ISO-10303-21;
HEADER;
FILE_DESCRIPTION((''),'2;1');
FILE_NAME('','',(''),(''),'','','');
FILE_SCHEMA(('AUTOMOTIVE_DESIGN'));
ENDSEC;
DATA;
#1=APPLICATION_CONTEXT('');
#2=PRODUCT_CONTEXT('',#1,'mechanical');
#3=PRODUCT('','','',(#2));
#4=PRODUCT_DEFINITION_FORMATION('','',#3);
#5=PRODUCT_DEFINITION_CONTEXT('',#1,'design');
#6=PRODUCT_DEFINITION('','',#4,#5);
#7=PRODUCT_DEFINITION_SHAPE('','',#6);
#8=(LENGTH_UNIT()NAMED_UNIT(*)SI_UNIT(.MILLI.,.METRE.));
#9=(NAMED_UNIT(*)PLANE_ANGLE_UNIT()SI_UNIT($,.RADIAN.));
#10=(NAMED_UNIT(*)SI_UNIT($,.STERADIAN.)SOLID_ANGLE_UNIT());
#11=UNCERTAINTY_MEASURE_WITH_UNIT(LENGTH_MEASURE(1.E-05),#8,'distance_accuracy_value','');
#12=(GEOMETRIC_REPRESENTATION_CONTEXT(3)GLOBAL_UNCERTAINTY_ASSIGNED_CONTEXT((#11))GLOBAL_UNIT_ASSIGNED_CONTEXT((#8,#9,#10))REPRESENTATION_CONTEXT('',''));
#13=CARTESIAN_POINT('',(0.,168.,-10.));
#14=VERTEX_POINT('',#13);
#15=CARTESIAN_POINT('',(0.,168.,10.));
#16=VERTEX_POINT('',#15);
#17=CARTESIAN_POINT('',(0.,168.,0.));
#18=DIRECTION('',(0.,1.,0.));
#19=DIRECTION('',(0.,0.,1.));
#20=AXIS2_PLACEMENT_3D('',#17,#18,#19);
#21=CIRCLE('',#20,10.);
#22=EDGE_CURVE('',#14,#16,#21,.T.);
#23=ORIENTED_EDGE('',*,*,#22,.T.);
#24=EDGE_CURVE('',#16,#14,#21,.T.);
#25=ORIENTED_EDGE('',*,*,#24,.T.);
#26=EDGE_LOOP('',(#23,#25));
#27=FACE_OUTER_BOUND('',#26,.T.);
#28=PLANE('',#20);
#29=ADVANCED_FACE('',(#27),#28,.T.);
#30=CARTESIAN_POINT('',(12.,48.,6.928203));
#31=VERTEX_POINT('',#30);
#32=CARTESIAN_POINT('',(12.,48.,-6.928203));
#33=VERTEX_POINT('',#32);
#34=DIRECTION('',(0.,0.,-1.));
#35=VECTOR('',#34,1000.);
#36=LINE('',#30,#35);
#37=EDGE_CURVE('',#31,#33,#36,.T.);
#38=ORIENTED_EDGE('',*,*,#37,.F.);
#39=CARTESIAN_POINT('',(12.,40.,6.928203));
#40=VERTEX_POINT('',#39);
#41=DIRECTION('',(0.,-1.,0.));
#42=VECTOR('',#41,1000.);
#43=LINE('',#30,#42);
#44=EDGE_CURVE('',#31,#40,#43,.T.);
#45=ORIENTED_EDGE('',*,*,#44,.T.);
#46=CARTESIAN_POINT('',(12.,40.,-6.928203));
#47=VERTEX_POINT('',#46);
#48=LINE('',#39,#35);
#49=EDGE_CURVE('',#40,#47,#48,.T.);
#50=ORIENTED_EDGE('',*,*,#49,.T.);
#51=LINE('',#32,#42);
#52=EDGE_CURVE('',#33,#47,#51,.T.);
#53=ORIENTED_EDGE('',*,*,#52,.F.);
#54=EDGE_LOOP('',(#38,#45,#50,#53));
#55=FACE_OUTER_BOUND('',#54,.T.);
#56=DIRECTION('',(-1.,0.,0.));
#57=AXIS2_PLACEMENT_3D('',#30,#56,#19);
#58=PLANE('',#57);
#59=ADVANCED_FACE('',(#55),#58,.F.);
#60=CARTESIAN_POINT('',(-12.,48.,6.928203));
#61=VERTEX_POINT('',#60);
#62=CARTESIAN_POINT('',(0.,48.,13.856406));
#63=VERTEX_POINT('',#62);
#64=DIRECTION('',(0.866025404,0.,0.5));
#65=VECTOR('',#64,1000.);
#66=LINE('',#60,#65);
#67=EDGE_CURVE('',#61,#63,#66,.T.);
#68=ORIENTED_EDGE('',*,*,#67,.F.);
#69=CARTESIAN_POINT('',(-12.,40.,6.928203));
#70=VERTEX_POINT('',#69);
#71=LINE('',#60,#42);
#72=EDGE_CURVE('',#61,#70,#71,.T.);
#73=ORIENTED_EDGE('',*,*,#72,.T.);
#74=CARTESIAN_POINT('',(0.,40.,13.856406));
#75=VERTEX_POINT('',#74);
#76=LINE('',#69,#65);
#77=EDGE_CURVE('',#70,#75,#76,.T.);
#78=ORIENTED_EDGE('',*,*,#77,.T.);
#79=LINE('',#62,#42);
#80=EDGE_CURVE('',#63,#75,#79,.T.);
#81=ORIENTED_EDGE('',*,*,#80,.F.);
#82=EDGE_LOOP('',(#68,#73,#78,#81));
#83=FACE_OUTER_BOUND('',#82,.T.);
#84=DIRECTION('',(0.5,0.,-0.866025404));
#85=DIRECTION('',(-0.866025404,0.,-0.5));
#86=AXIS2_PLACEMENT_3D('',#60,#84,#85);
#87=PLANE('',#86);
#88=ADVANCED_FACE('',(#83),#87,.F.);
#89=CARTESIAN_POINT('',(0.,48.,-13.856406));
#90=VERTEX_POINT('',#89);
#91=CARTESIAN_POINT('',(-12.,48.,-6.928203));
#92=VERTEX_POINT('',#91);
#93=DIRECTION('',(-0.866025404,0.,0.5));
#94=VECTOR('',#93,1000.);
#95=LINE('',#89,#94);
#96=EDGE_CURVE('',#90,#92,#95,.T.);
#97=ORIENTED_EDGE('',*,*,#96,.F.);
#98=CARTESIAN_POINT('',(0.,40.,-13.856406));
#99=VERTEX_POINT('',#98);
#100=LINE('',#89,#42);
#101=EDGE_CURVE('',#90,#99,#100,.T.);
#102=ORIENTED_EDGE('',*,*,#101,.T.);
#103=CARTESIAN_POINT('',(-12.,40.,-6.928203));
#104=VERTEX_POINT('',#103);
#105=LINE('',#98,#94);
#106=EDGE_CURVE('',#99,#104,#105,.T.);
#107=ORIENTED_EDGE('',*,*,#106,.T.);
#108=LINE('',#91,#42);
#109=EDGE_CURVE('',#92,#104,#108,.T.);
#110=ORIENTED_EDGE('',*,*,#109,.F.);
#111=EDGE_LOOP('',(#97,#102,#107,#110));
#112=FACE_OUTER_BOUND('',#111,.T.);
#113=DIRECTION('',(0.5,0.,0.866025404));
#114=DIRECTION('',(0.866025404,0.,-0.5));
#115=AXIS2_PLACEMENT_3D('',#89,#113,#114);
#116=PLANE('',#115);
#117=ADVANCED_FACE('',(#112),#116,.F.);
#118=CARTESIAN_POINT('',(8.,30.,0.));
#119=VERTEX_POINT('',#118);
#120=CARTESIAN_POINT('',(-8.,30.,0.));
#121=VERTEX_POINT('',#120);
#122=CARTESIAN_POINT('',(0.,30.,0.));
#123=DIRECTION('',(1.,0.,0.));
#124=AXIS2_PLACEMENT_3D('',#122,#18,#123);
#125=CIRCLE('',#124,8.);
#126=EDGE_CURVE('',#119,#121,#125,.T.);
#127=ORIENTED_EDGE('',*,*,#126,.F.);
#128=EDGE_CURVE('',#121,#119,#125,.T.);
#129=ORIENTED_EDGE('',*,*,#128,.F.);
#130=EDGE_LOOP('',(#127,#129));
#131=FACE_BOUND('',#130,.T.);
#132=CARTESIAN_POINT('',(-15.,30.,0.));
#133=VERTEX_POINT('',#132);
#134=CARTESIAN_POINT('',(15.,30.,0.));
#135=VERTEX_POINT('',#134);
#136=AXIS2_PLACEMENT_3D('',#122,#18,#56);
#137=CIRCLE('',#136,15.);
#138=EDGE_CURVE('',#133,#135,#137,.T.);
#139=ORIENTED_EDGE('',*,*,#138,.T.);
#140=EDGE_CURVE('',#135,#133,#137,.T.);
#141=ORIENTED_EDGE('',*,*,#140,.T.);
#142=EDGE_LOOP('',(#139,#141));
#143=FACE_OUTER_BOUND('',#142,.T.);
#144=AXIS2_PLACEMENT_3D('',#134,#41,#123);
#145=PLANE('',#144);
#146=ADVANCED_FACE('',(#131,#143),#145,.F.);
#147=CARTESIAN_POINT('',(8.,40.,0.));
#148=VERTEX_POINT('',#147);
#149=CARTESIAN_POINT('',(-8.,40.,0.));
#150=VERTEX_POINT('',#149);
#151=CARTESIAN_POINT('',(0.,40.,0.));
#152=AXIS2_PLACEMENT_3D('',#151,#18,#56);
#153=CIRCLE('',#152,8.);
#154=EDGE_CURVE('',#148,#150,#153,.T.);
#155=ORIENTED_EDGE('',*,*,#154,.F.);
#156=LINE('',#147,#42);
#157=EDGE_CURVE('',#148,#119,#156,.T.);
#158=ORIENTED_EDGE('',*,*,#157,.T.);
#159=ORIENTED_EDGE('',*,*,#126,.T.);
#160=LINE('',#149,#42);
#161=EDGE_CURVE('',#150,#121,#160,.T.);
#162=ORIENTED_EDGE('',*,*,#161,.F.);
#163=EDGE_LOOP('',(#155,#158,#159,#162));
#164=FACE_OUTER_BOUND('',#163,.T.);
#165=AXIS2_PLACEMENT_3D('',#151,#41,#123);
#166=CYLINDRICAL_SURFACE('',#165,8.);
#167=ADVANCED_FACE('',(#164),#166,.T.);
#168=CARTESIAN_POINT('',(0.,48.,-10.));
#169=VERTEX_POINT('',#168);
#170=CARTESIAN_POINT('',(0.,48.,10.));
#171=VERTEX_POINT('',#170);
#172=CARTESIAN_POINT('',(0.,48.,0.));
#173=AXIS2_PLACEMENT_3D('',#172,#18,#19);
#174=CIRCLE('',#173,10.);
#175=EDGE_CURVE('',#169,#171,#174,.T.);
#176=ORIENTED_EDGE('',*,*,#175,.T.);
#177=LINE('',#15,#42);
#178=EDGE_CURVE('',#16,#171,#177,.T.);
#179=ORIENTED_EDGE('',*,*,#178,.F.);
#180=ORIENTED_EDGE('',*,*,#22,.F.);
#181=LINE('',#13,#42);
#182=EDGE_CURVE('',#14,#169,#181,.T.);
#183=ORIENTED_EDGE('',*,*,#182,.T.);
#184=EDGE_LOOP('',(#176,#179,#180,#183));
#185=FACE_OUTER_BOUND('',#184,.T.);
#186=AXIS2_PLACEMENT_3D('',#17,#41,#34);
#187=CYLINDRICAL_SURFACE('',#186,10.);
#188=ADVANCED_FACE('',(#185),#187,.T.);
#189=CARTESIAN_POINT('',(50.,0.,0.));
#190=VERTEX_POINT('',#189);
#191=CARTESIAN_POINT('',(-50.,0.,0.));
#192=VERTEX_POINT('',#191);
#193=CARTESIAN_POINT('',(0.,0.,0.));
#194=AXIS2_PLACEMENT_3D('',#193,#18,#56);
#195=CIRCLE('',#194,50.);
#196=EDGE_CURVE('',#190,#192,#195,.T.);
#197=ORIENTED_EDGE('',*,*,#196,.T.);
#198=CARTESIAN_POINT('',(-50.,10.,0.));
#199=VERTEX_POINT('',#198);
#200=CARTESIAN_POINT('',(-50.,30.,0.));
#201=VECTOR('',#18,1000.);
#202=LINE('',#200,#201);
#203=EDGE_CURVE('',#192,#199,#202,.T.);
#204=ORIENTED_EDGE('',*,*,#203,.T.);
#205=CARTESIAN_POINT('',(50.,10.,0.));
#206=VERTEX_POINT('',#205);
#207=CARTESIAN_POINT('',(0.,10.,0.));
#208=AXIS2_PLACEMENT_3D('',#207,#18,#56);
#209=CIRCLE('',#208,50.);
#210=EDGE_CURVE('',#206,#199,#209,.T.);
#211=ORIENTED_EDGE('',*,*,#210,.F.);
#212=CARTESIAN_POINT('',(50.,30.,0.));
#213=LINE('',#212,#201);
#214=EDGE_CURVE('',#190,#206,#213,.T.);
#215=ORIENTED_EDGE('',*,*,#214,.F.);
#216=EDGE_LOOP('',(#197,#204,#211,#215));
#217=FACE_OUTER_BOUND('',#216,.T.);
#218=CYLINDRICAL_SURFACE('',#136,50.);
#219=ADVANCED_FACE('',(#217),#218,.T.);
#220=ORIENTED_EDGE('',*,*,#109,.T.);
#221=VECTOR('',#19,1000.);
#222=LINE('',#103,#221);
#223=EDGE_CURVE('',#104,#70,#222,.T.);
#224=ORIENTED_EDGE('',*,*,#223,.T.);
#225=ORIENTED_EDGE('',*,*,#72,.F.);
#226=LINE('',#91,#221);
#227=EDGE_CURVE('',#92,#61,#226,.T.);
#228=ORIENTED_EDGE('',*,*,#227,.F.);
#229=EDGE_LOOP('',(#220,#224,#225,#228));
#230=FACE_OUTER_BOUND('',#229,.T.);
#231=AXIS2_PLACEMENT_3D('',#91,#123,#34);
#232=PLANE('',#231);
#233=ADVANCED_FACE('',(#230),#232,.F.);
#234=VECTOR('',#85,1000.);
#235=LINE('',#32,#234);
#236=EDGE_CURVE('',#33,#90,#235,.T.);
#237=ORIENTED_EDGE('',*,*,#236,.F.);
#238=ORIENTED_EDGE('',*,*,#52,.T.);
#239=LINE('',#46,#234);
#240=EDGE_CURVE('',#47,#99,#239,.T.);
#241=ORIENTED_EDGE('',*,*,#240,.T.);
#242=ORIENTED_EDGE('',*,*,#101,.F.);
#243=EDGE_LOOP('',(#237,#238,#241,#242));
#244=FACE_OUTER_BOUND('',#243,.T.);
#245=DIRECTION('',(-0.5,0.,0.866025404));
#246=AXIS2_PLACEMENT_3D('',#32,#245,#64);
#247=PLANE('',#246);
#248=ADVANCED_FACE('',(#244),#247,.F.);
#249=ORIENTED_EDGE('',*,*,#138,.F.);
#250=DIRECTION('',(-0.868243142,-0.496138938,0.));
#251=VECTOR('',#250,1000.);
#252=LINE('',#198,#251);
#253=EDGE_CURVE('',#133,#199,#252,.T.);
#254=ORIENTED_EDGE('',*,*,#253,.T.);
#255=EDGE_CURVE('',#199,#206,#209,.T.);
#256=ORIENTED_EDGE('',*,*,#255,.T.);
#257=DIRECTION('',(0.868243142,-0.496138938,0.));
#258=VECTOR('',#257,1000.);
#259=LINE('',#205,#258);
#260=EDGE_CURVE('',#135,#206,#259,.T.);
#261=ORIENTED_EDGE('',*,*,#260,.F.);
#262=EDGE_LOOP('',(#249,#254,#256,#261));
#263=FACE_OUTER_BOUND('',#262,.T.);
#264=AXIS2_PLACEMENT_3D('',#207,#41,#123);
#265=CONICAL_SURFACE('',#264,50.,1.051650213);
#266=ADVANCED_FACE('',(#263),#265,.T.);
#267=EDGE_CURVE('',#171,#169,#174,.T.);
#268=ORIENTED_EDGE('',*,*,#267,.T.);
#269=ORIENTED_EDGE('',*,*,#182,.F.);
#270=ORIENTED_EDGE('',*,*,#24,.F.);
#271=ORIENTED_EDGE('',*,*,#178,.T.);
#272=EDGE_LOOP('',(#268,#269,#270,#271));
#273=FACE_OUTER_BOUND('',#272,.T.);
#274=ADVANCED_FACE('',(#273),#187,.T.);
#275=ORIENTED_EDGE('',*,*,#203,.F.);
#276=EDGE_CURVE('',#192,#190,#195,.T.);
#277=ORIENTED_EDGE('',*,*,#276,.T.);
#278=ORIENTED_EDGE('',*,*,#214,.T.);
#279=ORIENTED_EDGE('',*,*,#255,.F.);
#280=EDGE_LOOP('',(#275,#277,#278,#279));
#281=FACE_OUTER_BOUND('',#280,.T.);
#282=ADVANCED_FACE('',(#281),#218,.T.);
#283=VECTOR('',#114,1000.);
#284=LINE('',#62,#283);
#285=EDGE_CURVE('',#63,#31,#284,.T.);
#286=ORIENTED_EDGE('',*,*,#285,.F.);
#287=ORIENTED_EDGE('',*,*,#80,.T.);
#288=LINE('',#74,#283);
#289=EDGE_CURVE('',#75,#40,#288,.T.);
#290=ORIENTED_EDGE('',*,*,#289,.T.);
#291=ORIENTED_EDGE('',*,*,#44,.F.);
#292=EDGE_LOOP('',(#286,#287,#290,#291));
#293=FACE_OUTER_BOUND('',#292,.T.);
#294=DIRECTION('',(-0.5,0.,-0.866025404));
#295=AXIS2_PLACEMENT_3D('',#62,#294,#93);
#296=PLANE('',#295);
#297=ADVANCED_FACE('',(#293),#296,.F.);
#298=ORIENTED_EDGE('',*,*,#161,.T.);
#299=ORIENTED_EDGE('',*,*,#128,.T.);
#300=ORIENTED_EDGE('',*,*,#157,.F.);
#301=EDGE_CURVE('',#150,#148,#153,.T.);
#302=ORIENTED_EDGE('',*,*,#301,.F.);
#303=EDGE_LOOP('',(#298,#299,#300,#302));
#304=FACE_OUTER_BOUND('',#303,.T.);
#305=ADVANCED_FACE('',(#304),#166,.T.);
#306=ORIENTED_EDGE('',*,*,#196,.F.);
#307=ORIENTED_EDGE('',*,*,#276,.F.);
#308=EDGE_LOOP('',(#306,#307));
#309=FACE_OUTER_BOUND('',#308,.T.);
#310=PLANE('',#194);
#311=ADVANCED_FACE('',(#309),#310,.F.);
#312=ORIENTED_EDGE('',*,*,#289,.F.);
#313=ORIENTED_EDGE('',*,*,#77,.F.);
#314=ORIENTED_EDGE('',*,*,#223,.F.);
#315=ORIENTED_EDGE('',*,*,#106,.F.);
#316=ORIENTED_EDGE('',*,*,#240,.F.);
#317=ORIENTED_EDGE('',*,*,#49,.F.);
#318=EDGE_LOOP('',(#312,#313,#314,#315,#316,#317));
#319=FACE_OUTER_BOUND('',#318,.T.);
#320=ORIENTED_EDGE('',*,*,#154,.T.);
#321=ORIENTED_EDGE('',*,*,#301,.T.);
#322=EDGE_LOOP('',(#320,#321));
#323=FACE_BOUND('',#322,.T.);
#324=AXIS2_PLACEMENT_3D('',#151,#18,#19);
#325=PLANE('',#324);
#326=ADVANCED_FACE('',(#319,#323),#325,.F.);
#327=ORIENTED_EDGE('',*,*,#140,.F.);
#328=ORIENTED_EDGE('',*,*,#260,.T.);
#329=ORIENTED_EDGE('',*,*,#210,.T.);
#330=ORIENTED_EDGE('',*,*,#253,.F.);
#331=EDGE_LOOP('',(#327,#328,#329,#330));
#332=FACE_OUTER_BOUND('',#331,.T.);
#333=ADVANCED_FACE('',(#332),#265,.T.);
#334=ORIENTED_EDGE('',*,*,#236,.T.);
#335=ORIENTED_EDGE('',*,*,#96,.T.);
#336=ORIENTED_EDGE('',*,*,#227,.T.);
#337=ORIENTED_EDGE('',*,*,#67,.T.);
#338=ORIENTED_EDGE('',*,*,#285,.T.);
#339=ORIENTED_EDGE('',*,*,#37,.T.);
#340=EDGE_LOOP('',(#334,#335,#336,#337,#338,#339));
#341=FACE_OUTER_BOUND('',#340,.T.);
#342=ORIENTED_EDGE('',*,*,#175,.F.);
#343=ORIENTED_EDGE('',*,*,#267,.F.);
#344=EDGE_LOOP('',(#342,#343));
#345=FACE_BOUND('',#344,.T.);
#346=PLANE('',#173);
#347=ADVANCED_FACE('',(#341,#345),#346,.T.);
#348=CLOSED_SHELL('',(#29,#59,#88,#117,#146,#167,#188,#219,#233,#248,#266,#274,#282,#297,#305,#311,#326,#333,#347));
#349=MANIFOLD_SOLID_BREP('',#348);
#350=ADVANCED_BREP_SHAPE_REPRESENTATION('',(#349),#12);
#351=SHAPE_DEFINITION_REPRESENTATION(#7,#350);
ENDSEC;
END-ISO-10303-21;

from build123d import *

# Parameters (mm, degrees)
SKETCH_2_R      = 8
EXTRUDE_1_DEPTH = 10
EXTRUDE_2_DEPTH = 8
SKETCH_4_R      = 10
EXTRUDE_3_DEPTH = 120


with BuildPart() as part:
    # 草图1 → 旋转1 (revolve)
    with BuildSketch(Plane.XY, mode=Mode.PRIVATE) as revolve_1_sk:
        Polygon((0, 30), (0, 0), (50, 0), (50, 10), (15, 30), align=None)
    revolve(revolve_1_sk.sketch.rotate(Axis((0, 30, 0), (0, -1, 0)), 180), axis=Axis((0, 30, 0), (0, -1, 0)))

    # 草图2 → 凸台-拉伸1 (add)
    with BuildSketch(Plane(origin=(0, 30, 0), x_dir=(1, 0, 0), z_dir=(0, 1, 0))):
        Circle(SKETCH_2_R)
    extrude(amount=EXTRUDE_1_DEPTH)

    # 草图3 → 凸台-拉伸2 (add)
    with BuildSketch(Plane(origin=(0, 40, 0), x_dir=(1, 0, 0), z_dir=(0, 1, 0))):
        Polygon((0, 13.856406461), (-12, 6.92820323), (-12, -6.92820323), (0, -13.856406461), (12, -6.92820323), (12, 6.92820323), align=None)
    extrude(amount=EXTRUDE_2_DEPTH)

    # 草图4 → 凸台-拉伸3 (add)
    with BuildSketch(Plane(origin=(0, 48, 0), x_dir=(1, 0, 0), z_dir=(0, 1, 0))):
        with Locations(Location((0, 0, 0), (0, 0, 270))):
            Circle(SKETCH_4_R)
    extrude(amount=EXTRUDE_3_DEPTH)


solid = part.part
